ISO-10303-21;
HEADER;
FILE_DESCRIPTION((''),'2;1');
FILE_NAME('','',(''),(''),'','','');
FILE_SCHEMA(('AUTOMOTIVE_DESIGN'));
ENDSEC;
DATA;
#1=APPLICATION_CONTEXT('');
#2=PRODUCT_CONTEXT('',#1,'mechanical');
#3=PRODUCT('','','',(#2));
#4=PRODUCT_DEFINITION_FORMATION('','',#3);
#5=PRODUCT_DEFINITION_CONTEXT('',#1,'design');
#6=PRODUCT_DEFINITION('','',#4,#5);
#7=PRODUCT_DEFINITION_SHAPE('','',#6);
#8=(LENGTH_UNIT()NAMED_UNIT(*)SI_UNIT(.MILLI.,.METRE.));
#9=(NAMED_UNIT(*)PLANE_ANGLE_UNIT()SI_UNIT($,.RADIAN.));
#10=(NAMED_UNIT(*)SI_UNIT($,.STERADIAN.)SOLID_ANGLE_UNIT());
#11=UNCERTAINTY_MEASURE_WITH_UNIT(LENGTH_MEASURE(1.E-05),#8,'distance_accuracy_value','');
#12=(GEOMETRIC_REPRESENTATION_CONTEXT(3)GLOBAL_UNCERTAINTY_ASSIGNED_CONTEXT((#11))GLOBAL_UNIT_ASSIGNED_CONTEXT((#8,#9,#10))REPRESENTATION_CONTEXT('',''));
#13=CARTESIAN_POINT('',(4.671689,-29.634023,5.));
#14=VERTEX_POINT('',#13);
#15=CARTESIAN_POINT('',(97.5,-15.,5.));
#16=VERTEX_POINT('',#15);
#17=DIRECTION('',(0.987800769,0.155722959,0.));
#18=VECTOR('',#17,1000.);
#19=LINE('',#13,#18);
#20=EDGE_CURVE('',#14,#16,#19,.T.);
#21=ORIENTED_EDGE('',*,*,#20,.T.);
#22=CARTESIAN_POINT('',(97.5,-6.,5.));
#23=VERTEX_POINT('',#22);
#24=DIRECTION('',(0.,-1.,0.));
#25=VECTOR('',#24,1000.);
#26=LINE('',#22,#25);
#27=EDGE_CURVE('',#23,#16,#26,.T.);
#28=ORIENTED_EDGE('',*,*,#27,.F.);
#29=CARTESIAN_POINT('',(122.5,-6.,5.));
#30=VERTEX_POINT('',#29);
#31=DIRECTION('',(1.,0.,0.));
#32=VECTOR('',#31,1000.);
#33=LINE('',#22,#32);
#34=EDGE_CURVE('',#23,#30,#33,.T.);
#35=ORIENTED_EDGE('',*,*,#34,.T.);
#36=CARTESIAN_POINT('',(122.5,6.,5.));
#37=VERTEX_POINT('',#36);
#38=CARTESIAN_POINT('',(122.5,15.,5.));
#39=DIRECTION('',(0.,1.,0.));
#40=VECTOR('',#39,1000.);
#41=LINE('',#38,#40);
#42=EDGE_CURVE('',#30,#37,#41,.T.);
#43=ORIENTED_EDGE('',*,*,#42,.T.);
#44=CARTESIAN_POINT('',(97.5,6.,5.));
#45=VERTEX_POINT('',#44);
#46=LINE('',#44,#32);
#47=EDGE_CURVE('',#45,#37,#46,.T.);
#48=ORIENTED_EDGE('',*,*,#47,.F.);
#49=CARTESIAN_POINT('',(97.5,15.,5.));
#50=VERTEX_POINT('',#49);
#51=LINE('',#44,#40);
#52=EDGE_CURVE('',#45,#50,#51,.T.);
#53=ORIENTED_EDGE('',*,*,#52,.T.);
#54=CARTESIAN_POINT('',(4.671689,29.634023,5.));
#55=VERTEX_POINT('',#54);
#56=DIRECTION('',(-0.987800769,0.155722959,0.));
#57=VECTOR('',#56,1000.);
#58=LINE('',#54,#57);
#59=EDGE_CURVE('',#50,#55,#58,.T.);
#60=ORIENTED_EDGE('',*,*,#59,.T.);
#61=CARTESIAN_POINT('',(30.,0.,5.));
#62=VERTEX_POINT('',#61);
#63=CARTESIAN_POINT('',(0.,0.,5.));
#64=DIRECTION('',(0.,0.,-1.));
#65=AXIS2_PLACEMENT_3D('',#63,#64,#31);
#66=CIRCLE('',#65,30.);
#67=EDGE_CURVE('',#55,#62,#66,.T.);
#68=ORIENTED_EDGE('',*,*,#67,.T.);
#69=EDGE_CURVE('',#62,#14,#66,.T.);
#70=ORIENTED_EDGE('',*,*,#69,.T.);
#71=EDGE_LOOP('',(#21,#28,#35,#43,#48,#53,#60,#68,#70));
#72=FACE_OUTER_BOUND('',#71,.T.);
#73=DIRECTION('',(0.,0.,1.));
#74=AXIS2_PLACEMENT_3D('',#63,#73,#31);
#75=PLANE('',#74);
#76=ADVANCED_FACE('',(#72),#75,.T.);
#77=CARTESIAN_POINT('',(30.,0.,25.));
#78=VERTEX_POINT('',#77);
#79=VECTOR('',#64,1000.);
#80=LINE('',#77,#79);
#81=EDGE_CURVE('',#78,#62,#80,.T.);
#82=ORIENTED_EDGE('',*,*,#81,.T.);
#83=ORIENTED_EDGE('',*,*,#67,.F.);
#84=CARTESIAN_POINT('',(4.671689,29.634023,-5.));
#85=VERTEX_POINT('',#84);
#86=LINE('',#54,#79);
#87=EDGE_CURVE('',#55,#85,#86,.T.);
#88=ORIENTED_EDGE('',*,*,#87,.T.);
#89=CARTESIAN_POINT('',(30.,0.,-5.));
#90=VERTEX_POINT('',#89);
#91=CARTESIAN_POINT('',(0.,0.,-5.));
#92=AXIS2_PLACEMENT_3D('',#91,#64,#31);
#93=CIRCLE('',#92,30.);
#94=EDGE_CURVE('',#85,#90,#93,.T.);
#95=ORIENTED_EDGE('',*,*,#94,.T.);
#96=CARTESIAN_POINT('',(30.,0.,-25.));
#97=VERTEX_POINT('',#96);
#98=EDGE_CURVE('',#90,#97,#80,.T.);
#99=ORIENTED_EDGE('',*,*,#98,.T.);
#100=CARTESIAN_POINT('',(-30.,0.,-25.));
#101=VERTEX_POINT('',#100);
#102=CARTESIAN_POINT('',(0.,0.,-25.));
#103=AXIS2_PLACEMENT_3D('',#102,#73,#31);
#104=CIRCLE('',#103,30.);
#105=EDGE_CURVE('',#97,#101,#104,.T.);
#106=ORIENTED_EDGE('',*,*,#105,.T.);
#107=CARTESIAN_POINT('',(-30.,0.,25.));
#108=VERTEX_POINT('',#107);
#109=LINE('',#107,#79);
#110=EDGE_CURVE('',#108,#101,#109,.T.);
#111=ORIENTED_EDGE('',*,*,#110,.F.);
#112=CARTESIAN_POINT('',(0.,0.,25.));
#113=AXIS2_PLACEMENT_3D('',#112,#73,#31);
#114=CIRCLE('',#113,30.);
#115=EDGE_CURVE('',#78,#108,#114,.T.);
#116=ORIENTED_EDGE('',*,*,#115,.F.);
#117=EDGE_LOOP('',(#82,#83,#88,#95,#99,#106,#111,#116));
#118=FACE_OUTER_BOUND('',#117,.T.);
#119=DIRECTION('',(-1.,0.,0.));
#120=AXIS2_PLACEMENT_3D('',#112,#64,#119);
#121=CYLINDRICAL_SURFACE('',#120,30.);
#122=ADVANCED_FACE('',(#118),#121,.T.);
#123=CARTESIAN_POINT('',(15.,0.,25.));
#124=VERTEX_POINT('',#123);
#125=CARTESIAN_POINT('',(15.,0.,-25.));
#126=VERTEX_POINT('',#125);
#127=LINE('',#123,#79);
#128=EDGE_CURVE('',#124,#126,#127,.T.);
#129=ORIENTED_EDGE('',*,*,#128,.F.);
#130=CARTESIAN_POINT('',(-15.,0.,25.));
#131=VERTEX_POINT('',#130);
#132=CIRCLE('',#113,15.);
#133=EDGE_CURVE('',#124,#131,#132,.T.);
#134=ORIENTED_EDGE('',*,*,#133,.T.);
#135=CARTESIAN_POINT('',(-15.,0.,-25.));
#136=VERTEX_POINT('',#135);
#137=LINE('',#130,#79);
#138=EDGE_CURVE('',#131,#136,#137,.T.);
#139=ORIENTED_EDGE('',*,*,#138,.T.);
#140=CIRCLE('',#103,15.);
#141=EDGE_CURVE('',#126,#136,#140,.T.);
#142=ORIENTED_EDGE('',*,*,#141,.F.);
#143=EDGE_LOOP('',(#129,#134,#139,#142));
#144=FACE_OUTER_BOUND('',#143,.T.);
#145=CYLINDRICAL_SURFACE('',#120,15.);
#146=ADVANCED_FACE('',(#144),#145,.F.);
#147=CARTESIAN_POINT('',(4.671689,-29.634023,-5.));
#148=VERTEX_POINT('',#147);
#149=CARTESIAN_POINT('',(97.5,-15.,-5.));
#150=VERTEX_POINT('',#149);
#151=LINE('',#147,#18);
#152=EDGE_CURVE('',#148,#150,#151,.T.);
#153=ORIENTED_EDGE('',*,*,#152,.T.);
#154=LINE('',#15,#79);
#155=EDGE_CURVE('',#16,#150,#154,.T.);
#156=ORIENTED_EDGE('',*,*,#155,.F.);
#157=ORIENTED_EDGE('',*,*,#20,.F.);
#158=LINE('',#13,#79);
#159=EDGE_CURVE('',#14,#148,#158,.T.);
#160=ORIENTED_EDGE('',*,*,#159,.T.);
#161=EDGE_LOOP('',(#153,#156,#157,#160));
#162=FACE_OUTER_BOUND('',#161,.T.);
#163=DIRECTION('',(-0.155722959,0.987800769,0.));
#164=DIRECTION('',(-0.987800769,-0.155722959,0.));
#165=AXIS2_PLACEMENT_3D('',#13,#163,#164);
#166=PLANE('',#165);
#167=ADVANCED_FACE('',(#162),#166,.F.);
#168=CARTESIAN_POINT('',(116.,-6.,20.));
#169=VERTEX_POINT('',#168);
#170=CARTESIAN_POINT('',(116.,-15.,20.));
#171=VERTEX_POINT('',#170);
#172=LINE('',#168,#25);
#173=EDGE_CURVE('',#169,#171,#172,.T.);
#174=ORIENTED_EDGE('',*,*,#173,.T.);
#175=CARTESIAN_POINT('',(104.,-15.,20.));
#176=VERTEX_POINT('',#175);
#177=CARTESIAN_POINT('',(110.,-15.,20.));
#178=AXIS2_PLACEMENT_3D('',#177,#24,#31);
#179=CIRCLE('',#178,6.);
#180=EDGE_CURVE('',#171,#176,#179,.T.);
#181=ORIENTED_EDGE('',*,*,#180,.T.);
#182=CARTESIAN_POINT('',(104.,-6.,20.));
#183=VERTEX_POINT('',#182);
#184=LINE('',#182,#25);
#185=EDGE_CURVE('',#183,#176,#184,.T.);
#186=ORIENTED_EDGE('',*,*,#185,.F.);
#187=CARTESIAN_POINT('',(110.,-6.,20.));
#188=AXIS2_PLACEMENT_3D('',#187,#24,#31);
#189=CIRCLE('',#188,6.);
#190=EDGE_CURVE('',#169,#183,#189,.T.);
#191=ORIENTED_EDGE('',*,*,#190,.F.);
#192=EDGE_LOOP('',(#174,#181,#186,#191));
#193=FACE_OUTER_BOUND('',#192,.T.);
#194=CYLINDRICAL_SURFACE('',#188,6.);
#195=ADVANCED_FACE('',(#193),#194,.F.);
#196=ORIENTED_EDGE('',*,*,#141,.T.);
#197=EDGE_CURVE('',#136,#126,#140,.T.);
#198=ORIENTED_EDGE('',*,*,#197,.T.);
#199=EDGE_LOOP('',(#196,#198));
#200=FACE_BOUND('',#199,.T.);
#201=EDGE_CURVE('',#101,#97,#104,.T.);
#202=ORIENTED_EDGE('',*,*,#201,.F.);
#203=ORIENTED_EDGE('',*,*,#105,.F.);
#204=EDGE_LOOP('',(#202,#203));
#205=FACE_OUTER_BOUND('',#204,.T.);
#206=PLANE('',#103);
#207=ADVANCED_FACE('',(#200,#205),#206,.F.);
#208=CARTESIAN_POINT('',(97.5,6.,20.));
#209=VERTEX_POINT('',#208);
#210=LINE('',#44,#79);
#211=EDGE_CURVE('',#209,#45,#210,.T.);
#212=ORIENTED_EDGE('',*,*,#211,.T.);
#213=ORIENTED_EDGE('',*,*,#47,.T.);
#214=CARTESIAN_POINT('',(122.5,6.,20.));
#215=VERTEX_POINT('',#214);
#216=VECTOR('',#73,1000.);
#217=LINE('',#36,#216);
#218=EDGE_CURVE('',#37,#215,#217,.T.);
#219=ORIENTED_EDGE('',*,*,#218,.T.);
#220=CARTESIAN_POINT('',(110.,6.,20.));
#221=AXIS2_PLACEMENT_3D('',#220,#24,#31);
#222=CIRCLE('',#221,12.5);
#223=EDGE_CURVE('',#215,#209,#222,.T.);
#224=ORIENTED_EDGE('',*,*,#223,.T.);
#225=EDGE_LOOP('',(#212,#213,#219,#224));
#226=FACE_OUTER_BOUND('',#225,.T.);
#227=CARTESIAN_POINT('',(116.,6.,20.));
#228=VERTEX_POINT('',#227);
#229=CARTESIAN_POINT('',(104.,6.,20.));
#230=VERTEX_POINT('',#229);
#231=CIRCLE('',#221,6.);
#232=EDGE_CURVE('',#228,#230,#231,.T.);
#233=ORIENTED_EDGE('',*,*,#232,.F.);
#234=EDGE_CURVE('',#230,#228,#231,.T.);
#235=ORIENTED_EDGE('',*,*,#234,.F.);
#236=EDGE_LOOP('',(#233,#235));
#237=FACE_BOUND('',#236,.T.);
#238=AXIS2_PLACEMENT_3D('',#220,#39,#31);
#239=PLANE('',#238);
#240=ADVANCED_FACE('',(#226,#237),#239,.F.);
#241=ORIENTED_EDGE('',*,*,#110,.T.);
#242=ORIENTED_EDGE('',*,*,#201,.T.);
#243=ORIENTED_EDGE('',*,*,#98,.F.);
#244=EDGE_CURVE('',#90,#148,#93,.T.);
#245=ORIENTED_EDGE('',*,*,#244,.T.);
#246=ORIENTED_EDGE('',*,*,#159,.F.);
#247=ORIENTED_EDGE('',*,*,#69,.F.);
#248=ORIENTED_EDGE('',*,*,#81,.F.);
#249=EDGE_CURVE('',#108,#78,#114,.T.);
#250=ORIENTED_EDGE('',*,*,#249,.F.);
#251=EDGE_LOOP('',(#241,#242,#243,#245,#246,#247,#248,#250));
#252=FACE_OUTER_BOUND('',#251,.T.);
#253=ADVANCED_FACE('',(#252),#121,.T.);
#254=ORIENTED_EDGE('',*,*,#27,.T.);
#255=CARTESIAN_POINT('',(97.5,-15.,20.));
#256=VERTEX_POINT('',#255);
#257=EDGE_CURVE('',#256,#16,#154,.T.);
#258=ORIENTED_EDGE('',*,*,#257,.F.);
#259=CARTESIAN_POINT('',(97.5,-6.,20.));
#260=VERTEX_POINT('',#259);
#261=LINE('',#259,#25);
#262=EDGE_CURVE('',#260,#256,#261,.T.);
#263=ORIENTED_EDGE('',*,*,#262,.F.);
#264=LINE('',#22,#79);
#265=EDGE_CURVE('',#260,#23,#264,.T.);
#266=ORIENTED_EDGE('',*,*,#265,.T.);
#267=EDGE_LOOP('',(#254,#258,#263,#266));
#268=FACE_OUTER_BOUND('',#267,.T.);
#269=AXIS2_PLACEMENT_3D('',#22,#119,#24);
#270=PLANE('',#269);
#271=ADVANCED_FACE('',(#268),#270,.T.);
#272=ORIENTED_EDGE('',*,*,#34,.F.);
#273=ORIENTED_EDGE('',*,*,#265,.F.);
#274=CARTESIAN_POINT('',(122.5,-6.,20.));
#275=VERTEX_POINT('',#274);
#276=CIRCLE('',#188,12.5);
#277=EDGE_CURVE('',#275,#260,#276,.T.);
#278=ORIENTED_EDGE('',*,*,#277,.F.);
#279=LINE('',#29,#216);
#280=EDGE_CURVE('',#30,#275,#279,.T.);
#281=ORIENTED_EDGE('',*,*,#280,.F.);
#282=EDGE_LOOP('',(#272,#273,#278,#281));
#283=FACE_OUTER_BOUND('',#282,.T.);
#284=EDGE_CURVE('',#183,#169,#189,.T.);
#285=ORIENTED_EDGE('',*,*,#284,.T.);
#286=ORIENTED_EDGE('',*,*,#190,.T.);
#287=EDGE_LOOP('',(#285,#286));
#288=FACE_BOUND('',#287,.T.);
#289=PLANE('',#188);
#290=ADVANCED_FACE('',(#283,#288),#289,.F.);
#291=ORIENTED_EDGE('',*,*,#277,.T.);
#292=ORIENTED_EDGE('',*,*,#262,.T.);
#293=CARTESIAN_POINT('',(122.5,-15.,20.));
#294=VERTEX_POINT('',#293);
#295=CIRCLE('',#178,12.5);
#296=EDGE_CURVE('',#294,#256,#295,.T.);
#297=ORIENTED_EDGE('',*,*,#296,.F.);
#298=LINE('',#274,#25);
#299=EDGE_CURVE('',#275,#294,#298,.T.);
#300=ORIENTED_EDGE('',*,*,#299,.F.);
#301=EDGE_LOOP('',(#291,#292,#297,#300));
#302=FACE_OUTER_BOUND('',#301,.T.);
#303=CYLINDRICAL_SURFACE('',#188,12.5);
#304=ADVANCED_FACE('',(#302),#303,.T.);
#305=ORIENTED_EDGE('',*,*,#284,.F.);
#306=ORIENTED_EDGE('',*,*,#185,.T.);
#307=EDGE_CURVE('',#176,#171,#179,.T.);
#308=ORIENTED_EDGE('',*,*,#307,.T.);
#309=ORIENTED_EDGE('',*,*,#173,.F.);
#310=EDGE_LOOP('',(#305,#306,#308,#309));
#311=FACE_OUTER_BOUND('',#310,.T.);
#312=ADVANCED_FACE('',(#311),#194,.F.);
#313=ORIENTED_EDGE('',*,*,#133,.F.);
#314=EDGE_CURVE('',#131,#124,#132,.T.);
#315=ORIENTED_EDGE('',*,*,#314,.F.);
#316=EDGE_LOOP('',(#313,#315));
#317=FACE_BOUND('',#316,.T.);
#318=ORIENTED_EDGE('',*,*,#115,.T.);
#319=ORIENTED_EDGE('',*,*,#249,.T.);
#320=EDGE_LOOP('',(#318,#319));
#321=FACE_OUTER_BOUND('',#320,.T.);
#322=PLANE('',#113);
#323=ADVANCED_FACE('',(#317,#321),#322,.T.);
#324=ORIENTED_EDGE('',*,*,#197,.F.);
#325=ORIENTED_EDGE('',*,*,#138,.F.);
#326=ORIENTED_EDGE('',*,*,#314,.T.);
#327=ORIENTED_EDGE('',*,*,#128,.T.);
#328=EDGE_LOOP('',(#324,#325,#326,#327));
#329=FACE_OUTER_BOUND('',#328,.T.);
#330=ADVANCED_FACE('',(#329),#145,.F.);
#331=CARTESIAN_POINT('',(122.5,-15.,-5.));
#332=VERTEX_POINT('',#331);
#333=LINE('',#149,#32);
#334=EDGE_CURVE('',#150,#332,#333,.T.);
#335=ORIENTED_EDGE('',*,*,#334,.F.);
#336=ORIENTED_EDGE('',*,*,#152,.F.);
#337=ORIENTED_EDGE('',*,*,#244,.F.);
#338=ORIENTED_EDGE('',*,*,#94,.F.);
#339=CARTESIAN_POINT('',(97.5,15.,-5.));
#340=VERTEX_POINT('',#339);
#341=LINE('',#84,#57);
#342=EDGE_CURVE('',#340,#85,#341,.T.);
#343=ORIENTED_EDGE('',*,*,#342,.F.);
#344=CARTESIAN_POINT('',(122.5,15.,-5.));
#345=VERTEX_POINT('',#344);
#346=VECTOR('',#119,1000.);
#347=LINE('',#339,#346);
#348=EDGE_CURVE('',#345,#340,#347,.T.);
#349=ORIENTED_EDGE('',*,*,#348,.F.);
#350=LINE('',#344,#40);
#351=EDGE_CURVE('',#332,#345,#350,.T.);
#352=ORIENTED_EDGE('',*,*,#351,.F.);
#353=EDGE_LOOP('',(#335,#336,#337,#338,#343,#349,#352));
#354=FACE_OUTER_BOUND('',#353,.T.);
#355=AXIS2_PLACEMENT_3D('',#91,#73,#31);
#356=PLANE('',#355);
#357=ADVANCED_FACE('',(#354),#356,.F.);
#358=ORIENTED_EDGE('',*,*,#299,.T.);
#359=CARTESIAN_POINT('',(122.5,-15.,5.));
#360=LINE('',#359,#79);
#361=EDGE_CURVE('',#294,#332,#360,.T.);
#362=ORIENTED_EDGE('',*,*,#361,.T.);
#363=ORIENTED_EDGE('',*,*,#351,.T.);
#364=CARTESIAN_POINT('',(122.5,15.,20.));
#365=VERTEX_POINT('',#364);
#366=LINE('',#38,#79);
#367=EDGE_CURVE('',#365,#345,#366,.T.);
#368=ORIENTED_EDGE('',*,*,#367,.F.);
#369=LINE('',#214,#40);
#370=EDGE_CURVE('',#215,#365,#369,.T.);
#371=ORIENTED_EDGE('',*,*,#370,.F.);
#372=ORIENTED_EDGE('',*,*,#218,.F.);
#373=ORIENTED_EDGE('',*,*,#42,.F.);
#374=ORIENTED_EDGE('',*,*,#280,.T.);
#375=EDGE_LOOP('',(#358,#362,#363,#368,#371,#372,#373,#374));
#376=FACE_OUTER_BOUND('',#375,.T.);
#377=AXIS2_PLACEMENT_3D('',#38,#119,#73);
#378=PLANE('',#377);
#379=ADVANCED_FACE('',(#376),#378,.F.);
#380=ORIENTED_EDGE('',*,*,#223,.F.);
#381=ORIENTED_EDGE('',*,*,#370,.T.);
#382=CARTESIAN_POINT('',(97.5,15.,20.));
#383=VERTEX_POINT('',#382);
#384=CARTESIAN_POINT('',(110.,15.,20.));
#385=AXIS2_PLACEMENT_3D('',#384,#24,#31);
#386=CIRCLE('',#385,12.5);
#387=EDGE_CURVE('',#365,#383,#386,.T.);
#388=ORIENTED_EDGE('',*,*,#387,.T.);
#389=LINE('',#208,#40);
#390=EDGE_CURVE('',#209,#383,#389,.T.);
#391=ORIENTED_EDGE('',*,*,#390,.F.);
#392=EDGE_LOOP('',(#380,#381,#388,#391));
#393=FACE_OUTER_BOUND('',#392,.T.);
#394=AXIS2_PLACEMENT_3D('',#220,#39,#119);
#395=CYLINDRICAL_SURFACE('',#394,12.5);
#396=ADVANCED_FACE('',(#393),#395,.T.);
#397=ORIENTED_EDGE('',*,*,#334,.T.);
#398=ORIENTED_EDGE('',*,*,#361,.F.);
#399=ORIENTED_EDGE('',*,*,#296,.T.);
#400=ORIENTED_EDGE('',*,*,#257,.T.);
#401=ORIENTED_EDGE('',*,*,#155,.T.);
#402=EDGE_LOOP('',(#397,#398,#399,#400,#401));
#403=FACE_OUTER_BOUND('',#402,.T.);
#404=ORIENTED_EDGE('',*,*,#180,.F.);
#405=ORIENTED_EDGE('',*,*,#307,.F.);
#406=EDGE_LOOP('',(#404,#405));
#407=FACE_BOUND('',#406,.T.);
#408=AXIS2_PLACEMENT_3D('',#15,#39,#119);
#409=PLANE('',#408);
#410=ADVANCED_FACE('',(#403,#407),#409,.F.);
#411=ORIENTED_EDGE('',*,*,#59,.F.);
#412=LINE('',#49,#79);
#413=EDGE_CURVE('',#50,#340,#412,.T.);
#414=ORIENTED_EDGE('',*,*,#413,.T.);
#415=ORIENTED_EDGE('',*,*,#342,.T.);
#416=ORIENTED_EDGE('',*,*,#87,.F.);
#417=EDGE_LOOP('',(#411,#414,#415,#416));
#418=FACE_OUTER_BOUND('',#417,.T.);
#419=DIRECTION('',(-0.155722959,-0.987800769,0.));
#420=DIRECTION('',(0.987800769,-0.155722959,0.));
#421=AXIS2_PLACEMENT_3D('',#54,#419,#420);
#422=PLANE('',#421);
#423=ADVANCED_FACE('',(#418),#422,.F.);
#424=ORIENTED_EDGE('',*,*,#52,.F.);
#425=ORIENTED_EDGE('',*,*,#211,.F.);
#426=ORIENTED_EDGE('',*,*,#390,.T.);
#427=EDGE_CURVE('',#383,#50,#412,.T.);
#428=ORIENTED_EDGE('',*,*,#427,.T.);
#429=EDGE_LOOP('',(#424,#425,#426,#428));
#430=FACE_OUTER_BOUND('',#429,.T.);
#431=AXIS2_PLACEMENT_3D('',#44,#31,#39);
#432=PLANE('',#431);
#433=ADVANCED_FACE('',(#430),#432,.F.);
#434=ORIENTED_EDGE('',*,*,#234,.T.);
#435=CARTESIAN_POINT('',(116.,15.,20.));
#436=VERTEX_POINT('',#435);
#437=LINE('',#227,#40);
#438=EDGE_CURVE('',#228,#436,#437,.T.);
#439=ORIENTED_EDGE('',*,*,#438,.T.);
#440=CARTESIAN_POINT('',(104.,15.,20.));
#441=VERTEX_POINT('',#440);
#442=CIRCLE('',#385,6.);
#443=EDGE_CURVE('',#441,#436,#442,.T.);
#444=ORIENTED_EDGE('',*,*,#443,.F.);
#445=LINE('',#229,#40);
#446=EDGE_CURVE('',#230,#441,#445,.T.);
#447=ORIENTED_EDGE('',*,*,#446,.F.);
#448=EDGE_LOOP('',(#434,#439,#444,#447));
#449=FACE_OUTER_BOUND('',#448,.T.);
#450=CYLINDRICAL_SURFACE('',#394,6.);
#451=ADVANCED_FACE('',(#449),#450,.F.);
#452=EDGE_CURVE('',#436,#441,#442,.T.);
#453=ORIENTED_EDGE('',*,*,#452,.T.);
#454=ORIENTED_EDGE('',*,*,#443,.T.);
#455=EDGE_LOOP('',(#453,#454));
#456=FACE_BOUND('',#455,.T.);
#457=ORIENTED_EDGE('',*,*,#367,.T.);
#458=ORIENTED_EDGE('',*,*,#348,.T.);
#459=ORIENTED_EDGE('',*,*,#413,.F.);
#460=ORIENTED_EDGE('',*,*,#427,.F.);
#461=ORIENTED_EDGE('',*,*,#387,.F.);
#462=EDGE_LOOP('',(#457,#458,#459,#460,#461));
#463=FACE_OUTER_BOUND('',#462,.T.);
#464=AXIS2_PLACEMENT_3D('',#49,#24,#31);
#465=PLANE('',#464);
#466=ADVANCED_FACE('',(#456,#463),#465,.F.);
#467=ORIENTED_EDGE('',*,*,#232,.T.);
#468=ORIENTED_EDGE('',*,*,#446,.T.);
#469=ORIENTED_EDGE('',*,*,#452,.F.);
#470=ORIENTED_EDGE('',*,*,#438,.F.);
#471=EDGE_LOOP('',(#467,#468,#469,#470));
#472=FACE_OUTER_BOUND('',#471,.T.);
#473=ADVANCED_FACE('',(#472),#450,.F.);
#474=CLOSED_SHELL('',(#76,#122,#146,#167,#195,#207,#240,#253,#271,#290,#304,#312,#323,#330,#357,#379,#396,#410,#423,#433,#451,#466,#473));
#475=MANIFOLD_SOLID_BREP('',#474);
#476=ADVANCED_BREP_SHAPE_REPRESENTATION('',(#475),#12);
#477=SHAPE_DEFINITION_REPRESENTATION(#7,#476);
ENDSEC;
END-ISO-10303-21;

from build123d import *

# Parameters (mm, degrees)
HUB_PROFILE_SKETCH_R   = 30
HUB_PROFILE_SKETCH_R_2 = 15
HUB_60_BORE_30_DEPTH   = 25
LEVER_ARM_WEB_DEPTH    = 5
CLEVIS_LUG_SKETCH_R    = 6
CLEVIS_LUG_DEPTH       = 9


with BuildPart() as part:
    # Hub Profile Sketch → Hub Ø60 Bore Ø30 (new, symmetric)
    with BuildSketch(Plane.XY):
        Circle(HUB_PROFILE_SKETCH_R)
        Circle(HUB_PROFILE_SKETCH_R_2, mode=Mode.SUBTRACT)
    extrude(amount=HUB_60_BORE_30_DEPTH, both=True)

    # Lever Arm Sketch → Lever Arm Web (add, symmetric)
    with BuildSketch(Plane.XY):
        with BuildLine():
            Line((4.671688756, 29.634023084), (97.5, 15))
            Line((97.5, 15), (122.5, 15))
            Line((122.5, 15), (122.5, -15))
            Line((122.5, -15), (97.5, -15))
            Line((97.5, -15), (4.671688756, -29.634023084))
            ThreePointArc((4.671688756, -29.634023084), (30, 0), (4.671688756, 29.634023084))
        make_face()
    extrude(amount=LEVER_ARM_WEB_DEPTH, both=True)

    # Clevis Lug Sketch → Clevis Lug (add)
    with BuildSketch(Plane.XZ.offset(15)):
        with BuildLine():
            Line((97.5, 5), (97.5, 20))
            ThreePointArc((97.5, 20), (110, 32.5), (122.5, 20))
            Line((122.5, 20), (122.5, 5))
            Line((122.5, 5), (97.5, 5))
        make_face()
        with Locations((110, 20)):
            Circle(CLEVIS_LUG_SKETCH_R, mode=Mode.SUBTRACT)
    clevis_lug = extrude(amount=-CLEVIS_LUG_DEPTH)

    # Clevis Lug Mirror: Clevis Lug across plane
    add(clevis_lug.mirror(Plane.ZX))


solid = part.part
